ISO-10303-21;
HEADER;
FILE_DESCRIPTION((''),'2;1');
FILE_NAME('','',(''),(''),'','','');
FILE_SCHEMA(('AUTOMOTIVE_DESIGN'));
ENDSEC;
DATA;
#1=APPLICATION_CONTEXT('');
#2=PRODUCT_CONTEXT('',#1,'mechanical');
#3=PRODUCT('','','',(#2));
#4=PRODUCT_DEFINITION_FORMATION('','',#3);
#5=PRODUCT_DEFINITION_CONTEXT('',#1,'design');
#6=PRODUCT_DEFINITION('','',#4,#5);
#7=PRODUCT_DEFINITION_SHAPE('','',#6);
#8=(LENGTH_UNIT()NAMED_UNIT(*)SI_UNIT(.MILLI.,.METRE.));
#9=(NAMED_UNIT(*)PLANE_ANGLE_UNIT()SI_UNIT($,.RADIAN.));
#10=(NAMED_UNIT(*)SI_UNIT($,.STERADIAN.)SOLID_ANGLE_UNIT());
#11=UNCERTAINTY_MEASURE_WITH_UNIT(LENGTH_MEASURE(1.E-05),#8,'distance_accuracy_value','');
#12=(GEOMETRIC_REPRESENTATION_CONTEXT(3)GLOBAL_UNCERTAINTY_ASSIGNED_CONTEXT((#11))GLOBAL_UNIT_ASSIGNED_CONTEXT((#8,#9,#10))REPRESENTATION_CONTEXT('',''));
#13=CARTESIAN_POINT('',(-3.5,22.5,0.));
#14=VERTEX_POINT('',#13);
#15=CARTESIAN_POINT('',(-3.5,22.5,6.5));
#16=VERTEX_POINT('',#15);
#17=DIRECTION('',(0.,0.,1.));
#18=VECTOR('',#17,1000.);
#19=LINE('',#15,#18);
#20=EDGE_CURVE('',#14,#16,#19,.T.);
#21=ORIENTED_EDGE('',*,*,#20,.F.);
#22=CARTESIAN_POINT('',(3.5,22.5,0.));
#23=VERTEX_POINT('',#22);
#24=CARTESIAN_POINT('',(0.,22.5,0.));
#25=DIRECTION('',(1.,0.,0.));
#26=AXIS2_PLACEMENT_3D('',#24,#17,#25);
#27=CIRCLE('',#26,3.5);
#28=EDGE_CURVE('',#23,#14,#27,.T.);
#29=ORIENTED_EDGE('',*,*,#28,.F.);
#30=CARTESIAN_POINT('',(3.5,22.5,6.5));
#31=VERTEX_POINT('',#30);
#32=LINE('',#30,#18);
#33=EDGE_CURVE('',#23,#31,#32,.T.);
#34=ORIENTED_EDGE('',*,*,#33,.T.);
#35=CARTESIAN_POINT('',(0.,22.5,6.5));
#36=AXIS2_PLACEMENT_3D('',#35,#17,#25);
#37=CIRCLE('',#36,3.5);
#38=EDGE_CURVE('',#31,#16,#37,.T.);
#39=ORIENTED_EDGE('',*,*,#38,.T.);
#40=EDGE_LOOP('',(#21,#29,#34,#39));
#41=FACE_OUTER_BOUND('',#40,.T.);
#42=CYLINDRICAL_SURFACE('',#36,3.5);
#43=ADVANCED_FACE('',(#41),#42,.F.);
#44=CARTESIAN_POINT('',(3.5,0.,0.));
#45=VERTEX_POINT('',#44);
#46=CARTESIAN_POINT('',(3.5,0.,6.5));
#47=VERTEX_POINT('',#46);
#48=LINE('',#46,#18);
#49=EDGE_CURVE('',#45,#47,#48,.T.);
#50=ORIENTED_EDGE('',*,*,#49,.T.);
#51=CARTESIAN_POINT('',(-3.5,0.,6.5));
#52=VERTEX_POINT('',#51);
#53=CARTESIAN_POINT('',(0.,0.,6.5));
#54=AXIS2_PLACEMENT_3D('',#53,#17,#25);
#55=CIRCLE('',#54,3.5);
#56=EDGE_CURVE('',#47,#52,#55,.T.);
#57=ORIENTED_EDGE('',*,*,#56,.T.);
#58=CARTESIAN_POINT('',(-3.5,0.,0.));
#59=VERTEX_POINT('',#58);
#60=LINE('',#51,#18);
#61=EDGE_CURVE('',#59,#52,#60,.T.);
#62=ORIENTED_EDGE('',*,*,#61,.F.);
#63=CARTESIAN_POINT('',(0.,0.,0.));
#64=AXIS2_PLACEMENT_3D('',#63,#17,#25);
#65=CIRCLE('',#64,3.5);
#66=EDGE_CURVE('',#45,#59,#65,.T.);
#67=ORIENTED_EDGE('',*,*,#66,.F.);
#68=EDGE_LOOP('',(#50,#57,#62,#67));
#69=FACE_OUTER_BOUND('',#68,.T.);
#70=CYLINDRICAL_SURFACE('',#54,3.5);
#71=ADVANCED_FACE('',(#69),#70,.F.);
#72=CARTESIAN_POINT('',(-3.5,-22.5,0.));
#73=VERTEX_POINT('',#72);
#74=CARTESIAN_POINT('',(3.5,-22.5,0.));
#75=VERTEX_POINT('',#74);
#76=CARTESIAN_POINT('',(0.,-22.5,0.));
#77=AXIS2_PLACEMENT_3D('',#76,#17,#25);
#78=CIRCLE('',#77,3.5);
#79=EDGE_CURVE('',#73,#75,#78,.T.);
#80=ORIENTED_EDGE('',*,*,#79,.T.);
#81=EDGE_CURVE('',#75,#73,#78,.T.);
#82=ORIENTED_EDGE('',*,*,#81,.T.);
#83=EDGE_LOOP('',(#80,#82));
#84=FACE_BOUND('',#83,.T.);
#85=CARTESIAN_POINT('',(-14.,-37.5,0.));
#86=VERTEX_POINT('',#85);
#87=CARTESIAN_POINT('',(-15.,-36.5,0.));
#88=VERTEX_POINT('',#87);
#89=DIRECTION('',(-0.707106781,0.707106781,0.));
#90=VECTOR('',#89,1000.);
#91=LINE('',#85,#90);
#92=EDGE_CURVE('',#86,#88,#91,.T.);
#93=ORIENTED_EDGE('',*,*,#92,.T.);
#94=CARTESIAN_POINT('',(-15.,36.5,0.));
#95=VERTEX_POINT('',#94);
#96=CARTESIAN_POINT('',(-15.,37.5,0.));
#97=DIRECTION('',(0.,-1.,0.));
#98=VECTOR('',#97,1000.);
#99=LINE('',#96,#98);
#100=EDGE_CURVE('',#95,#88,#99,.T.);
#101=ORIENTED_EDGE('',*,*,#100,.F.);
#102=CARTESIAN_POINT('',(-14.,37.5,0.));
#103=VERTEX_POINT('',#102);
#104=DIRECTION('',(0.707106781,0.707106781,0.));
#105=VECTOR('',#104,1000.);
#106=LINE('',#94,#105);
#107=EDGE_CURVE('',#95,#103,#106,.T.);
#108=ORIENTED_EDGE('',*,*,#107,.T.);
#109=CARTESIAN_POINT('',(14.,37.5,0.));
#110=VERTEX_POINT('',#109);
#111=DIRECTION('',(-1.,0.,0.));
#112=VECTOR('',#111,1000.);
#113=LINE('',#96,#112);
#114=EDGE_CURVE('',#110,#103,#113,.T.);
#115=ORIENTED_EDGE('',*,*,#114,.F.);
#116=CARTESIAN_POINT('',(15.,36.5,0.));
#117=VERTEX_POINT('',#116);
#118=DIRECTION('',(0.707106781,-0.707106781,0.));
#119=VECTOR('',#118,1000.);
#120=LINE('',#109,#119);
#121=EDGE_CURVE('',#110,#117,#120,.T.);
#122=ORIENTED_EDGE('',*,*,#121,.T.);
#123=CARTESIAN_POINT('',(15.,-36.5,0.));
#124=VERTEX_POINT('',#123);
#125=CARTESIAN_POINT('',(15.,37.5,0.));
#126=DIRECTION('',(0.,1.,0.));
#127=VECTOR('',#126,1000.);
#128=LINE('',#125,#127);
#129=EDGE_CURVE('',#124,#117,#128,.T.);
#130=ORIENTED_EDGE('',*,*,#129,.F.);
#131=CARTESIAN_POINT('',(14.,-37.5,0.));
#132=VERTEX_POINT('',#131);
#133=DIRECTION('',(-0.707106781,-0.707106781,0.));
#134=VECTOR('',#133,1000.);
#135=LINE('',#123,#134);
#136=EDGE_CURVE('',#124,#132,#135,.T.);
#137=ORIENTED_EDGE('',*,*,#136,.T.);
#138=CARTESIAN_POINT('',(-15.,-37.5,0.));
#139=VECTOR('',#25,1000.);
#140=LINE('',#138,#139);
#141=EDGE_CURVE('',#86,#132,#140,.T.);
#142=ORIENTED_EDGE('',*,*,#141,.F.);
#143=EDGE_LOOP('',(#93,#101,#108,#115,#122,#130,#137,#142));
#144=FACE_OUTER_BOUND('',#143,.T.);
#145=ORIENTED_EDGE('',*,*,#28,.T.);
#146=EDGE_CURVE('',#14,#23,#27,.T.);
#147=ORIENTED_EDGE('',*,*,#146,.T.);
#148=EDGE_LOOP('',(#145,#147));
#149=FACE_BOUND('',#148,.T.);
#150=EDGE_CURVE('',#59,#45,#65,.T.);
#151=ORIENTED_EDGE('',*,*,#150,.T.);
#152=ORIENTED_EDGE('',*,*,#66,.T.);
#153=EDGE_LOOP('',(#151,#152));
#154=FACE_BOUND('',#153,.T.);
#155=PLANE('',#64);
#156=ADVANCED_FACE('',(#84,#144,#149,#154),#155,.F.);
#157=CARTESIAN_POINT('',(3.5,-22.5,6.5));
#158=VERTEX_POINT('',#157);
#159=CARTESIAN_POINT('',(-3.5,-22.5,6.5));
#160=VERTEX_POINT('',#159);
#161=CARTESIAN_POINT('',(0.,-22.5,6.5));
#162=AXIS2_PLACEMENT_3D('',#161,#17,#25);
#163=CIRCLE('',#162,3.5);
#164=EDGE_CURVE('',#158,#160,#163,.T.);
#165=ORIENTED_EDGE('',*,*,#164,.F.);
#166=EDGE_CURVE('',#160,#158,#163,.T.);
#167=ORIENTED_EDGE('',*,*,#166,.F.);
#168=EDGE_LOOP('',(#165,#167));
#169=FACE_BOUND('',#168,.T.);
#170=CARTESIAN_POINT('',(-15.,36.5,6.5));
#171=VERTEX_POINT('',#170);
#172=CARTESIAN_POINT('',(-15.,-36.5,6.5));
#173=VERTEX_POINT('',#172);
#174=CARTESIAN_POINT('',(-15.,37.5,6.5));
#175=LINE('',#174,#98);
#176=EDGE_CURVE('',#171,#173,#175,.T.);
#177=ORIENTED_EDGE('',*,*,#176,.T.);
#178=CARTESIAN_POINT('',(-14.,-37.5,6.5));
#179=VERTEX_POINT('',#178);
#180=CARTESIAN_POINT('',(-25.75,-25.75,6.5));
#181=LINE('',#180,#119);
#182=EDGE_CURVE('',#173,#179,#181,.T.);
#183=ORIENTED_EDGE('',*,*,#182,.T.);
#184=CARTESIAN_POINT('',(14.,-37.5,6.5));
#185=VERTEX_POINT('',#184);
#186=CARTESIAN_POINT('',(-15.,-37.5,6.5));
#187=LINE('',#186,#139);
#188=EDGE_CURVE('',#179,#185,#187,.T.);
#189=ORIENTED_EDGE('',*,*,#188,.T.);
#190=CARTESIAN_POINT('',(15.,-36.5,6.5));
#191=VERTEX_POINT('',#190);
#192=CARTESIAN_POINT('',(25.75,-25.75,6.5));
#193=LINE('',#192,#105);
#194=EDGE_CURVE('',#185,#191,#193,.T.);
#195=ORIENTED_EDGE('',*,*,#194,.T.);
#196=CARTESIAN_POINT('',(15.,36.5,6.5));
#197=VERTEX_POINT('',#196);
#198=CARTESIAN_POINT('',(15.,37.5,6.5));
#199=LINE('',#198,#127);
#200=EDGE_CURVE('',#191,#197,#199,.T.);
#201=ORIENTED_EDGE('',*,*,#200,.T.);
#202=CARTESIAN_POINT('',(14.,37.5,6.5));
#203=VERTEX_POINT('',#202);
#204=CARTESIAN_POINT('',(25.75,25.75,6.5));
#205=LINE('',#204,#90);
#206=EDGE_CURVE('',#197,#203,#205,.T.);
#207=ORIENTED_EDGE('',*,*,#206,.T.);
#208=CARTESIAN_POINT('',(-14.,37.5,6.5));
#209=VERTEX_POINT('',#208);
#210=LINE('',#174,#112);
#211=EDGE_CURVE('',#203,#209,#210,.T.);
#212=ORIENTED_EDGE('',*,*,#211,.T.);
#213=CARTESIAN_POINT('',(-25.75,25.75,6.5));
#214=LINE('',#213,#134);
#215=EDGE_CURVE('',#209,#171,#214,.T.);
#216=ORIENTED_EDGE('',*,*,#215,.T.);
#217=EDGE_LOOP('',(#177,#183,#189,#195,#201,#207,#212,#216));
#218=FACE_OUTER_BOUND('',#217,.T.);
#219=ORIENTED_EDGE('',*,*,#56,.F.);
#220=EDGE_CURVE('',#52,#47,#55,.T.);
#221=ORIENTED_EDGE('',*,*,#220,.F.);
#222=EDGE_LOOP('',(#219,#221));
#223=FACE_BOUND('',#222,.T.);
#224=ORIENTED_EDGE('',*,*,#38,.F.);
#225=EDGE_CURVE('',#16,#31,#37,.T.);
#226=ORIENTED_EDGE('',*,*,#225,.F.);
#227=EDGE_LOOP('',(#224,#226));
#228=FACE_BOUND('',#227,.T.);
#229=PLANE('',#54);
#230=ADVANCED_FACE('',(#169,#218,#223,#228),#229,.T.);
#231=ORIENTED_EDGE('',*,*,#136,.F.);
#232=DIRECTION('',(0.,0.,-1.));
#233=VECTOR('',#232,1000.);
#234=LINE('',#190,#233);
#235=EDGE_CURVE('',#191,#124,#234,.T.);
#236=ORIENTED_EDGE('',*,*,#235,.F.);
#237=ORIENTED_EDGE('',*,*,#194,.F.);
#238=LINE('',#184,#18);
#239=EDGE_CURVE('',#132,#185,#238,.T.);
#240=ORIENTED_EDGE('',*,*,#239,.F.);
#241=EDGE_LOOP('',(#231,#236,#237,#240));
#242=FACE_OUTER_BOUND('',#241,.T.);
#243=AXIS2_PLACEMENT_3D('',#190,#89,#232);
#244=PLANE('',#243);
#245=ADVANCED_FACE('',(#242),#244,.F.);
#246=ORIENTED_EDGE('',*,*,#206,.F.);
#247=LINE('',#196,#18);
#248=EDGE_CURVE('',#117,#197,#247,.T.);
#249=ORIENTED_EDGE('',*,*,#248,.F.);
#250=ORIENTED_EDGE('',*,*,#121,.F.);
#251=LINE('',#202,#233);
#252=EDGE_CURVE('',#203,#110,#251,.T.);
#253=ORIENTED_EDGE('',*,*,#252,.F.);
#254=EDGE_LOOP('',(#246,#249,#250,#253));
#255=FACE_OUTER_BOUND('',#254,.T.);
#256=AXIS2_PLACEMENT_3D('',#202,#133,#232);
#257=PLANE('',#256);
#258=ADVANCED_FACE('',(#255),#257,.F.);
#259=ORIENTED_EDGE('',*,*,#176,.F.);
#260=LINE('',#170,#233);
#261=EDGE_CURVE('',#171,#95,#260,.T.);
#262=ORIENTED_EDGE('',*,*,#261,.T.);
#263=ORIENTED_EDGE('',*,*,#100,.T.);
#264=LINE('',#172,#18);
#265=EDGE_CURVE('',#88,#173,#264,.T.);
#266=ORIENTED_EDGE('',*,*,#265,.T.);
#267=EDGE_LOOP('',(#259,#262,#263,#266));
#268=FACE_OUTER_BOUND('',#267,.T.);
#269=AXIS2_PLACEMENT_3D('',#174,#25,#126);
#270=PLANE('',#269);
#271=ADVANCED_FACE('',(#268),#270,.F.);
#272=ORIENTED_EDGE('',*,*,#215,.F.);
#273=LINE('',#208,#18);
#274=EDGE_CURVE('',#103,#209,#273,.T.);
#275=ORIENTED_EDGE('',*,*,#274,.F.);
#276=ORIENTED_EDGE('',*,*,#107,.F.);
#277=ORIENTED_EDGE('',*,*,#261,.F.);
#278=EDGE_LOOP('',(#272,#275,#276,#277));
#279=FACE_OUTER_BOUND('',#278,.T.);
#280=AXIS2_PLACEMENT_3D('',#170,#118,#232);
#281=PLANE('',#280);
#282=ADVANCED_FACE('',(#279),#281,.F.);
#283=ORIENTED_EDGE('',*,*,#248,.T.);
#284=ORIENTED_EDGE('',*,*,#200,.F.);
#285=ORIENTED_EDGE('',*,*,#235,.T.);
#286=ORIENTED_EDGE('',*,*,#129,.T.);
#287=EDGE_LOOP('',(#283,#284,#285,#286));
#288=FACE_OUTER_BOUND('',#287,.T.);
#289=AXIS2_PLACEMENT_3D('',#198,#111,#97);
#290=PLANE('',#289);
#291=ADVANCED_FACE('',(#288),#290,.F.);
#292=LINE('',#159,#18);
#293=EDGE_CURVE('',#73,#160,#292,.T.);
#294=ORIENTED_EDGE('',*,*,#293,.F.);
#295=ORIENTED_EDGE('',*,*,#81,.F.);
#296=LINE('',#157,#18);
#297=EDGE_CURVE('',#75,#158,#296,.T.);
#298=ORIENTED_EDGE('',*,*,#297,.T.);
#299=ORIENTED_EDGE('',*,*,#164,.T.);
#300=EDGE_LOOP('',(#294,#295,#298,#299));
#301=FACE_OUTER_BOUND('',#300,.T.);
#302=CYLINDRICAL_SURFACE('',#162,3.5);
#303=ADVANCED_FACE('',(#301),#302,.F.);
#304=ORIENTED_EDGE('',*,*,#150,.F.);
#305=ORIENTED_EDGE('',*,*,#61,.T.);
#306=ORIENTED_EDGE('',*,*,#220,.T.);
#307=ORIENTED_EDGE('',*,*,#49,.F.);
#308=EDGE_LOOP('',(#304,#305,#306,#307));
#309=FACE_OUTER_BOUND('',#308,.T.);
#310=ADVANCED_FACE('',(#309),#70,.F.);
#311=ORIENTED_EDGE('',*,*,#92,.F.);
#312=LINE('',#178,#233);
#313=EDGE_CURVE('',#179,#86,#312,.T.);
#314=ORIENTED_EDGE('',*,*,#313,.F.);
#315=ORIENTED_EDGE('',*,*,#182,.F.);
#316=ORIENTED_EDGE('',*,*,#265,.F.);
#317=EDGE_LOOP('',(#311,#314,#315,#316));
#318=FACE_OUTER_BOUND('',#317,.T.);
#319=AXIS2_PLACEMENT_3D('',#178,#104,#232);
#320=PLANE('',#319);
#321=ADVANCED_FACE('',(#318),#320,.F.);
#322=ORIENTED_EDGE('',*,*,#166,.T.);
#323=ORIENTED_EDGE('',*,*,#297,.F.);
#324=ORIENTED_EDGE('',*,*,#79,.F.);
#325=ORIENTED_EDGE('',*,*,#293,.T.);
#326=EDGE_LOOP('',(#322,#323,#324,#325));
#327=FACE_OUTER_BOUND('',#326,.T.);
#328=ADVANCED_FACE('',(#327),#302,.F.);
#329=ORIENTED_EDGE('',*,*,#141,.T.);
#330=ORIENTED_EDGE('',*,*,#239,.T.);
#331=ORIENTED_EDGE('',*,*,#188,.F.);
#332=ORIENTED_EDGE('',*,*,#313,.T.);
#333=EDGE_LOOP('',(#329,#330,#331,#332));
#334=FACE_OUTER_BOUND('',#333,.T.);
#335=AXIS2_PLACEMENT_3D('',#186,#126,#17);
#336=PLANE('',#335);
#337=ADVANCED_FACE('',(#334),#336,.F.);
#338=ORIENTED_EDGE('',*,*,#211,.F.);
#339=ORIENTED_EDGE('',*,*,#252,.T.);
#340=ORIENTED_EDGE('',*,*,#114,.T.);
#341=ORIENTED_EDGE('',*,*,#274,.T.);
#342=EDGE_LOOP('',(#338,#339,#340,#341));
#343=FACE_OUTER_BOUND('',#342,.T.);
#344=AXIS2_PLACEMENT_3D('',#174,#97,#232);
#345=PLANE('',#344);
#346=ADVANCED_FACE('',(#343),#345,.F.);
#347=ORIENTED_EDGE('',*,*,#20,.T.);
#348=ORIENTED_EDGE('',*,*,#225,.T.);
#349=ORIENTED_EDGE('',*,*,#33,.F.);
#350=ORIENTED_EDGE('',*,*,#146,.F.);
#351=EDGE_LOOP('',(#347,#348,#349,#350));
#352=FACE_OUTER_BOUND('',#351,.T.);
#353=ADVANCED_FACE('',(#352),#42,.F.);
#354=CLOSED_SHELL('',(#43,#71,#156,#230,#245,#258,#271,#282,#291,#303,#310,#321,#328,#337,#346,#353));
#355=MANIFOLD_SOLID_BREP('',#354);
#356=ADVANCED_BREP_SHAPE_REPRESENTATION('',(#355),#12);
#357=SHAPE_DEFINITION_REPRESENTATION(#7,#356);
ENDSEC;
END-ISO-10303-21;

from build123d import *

# Parameters (mm, degrees)
SKETCH_1_W            = 30
SKETCH_1_H            = 75
EXTRUDE_1_DEPTH       = 6.5
HOLE_WIZARD_7_0_7_1_D = 7
CHAMFER_1_SIZE        = 1


with BuildPart() as part:
    # 草图1 → 凸台-拉伸1 (new body)
    with BuildSketch(Plane.XY):
        Rectangle(SKETCH_1_W, SKETCH_1_H)
    extrude(amount=EXTRUDE_1_DEPTH)

    # Ø7.0 (7) 直径孔1 (through all)
    with Locations(Plane.XY.offset(6.5)):
        with Locations((0, 0), (0, -22.5), (0, 22.5)):
            Hole(HOLE_WIZARD_7_0_7_1_D / 2)

    # 倒角1
    chamfer_1_edges = [part.edges().sort_by_distance(p)[0] for p in [
        (15, -37.5, 3.25),
        (-15, -37.5, 3.25),
        (-15, 37.5, 3.25),
        (15, 37.5, 3.25),
    ]]
    chamfer(chamfer_1_edges, length=CHAMFER_1_SIZE)


solid = part.part
